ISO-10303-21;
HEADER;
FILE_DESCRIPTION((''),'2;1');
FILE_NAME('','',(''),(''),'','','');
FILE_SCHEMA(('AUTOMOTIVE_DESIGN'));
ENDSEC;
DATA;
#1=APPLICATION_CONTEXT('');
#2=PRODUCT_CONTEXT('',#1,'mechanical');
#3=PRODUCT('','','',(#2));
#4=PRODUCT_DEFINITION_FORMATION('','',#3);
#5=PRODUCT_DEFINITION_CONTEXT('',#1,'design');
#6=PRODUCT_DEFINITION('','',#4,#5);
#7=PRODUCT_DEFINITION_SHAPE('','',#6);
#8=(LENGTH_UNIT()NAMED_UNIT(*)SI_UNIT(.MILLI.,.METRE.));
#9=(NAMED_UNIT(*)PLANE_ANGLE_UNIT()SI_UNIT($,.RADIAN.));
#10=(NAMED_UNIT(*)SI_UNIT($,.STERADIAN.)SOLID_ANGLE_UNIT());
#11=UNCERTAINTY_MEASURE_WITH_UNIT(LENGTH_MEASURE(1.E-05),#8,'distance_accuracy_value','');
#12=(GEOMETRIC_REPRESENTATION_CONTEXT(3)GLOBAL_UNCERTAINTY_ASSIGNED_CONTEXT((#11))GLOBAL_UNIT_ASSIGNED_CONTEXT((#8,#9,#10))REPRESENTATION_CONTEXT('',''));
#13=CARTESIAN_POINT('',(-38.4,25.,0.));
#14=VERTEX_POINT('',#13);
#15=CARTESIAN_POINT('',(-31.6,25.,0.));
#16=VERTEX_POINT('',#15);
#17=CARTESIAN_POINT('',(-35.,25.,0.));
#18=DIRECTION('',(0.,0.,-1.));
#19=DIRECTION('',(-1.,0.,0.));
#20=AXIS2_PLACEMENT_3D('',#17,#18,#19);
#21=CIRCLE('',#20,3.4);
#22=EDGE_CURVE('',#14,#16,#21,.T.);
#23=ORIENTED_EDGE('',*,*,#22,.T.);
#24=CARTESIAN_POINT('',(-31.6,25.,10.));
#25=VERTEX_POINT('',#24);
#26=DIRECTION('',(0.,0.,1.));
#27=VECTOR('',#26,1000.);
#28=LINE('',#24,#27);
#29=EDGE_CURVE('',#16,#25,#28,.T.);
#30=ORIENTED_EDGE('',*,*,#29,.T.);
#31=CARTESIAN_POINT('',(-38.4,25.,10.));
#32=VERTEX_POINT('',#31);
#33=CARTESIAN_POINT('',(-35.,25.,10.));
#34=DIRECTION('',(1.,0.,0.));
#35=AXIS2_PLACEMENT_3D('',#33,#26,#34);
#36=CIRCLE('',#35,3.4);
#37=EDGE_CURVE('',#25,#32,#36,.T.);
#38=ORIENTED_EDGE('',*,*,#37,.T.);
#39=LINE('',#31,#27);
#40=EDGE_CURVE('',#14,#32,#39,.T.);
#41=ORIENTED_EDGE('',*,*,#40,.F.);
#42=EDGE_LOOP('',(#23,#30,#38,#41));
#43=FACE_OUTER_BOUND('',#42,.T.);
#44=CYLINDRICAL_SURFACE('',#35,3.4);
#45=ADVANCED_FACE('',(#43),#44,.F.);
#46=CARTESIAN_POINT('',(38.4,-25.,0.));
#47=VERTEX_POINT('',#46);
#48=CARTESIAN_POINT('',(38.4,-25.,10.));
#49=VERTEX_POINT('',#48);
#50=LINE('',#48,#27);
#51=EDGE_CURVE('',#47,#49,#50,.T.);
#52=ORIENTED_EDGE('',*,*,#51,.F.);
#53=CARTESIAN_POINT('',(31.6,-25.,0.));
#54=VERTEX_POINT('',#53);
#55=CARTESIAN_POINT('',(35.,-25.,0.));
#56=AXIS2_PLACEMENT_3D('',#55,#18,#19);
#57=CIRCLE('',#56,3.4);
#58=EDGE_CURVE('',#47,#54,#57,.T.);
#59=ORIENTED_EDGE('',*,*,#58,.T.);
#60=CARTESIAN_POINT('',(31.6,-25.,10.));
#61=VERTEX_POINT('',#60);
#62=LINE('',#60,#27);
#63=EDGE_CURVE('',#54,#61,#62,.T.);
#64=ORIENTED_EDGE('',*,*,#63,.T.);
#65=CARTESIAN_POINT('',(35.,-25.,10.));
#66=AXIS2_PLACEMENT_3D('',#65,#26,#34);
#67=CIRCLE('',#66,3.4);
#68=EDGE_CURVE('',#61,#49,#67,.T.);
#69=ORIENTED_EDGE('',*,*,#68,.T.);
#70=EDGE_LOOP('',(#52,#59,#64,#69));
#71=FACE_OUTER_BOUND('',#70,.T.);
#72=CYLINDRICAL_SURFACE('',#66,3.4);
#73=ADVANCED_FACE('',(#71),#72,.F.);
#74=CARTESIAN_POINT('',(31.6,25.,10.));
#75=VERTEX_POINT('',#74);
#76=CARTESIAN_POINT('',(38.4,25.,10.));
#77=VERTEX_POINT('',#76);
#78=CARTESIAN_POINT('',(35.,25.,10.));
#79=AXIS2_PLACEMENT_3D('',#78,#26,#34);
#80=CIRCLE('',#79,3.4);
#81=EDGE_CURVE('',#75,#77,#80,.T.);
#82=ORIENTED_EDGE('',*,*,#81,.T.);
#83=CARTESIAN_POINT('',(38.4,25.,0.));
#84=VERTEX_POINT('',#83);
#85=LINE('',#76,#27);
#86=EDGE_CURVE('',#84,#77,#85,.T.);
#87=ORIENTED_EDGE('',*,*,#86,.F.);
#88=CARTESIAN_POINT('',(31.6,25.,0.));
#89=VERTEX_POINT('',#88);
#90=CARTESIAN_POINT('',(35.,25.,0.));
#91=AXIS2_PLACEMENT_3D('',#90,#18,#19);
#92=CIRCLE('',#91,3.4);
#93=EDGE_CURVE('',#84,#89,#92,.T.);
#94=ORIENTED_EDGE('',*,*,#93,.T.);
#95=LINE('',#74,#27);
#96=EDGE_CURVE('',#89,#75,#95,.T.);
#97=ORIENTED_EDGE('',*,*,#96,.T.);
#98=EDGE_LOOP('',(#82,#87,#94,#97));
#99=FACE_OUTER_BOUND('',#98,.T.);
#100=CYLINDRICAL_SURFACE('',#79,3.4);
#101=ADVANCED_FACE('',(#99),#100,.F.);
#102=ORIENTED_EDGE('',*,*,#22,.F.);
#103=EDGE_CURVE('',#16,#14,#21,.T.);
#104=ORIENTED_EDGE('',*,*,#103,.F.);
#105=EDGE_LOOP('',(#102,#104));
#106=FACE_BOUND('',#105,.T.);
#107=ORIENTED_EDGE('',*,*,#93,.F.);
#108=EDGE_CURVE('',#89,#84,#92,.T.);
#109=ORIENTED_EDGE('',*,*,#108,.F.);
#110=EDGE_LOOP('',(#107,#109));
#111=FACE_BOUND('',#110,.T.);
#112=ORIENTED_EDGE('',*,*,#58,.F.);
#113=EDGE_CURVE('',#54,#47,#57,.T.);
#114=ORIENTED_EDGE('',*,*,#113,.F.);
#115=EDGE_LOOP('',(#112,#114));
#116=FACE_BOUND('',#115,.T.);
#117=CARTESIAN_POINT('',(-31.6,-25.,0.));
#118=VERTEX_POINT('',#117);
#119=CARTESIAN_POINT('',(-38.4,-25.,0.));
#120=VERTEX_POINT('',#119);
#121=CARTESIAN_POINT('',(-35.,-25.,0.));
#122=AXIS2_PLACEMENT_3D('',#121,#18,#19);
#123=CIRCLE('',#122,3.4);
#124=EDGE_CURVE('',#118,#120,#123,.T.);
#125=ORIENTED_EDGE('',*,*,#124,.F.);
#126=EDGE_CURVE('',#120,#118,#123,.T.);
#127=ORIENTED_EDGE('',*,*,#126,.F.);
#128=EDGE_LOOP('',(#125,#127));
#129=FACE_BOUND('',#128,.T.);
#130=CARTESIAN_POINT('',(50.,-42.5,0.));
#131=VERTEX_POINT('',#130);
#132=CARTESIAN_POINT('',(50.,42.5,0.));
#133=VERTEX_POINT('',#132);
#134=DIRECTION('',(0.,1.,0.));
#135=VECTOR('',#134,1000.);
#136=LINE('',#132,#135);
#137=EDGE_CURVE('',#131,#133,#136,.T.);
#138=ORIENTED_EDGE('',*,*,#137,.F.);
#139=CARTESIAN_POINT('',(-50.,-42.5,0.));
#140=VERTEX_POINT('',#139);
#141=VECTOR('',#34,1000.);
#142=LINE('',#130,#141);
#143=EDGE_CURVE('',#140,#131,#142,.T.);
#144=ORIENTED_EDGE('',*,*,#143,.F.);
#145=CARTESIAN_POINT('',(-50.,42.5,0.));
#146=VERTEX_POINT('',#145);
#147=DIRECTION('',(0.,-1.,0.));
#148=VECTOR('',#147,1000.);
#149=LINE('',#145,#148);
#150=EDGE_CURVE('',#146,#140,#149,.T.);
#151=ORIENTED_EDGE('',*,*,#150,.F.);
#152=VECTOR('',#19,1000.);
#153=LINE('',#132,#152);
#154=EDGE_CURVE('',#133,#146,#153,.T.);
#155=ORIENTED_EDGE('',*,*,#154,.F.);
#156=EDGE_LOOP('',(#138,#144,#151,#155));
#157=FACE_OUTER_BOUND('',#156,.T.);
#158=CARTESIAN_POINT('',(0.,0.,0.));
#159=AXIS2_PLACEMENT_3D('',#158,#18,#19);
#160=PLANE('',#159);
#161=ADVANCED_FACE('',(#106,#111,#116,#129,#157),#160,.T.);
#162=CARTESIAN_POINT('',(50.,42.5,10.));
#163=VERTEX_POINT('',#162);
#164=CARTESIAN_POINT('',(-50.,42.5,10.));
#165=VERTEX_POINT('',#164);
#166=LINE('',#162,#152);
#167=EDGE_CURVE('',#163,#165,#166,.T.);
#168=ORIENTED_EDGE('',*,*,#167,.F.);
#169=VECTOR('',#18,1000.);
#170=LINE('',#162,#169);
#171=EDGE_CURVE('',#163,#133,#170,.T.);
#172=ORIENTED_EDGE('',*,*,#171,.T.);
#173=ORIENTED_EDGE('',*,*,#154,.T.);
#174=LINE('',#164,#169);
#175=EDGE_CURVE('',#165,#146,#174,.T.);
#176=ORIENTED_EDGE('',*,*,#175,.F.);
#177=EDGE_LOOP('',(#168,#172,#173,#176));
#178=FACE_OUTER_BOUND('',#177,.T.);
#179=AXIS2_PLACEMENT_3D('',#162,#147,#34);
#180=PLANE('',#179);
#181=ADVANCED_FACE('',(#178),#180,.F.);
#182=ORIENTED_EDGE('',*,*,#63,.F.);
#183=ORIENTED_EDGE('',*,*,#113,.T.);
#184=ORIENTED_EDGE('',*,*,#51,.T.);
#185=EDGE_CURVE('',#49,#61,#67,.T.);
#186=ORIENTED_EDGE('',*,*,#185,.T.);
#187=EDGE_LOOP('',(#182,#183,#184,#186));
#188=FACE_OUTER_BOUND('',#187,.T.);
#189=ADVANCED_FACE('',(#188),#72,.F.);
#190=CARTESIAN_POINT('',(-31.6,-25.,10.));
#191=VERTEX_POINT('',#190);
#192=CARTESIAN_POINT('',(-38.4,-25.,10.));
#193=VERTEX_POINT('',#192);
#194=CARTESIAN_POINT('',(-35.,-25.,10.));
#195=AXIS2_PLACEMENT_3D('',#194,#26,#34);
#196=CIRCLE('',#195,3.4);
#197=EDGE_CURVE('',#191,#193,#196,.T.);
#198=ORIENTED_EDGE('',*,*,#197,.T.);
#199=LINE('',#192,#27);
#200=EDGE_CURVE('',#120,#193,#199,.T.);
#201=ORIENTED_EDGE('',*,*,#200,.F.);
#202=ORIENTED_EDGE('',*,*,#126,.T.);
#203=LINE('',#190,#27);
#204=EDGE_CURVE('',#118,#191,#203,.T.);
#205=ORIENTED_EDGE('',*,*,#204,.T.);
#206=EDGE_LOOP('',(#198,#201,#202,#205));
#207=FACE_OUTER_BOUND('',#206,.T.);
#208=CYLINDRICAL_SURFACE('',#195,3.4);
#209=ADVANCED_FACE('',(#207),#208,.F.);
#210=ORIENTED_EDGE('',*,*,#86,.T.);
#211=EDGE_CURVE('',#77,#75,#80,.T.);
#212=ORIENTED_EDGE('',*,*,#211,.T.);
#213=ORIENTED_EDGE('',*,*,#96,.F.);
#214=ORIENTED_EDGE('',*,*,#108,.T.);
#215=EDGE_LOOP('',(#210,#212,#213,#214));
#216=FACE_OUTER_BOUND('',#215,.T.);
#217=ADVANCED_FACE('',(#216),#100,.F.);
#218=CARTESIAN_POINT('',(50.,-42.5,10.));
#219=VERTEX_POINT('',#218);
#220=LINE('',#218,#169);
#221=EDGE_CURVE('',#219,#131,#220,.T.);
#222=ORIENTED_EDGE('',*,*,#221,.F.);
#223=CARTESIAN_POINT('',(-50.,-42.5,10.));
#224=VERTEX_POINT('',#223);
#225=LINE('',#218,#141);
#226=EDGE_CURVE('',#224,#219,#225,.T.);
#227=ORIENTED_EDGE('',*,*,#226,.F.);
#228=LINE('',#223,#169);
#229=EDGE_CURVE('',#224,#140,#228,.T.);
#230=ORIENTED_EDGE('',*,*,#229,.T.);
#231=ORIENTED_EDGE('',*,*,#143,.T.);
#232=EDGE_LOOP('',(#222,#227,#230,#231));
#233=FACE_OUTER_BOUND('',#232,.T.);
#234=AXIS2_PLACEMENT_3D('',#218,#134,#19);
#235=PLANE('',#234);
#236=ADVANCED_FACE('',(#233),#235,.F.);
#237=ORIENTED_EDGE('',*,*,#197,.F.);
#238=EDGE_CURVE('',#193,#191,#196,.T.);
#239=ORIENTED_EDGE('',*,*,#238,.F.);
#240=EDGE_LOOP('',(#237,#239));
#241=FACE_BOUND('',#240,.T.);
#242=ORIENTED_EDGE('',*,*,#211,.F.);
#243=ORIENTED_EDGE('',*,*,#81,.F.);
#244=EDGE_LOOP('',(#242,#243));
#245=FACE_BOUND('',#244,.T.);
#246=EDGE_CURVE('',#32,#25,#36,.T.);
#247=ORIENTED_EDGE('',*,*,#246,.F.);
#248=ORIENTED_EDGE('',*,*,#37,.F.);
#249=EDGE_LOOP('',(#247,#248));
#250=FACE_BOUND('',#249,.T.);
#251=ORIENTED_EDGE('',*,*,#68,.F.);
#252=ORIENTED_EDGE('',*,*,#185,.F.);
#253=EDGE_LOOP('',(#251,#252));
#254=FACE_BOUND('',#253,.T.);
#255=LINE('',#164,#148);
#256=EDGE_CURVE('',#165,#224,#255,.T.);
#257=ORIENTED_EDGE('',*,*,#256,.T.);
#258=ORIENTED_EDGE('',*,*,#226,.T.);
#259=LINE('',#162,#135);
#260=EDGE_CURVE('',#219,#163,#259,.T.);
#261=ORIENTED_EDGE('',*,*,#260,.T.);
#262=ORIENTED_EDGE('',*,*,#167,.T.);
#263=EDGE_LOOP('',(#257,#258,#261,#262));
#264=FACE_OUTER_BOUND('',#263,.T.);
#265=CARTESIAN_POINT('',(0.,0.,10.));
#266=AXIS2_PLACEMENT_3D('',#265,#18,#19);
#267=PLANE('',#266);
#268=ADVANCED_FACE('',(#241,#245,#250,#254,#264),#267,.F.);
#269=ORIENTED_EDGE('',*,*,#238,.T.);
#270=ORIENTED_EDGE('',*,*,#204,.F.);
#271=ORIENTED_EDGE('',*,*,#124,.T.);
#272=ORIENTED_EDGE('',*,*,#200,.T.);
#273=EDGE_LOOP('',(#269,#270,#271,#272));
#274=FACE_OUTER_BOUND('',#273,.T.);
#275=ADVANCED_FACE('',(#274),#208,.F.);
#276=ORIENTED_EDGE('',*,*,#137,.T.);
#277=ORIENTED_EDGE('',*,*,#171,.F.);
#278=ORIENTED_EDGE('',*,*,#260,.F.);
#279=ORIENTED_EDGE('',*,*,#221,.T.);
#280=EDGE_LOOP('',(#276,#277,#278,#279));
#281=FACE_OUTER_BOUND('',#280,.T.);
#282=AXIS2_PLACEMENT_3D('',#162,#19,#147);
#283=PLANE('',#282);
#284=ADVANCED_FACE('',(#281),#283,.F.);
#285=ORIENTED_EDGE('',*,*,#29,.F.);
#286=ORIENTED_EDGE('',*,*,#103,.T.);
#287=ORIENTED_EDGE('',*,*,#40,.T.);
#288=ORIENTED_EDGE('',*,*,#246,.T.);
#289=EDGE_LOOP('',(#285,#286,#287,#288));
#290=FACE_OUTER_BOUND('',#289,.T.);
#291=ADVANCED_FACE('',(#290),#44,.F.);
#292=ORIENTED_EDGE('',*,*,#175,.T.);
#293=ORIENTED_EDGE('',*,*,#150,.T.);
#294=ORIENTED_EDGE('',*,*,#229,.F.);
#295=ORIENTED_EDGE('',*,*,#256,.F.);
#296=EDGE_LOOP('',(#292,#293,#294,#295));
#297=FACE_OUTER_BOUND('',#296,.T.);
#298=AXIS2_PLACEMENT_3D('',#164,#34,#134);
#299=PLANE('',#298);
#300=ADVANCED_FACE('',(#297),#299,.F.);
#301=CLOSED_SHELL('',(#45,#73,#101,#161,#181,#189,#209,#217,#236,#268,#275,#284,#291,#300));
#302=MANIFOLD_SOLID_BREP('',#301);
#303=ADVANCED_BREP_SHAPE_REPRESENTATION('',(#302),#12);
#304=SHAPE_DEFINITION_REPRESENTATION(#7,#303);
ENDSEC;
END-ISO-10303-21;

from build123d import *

# Parameters (mm, degrees)
SKETCH1_W             = 100
SKETCH1_H             = 85
BOSS_EXTRUDE1_DEPTH   = 10
M8_TAPPED_HOLE1_D     = 6.8
M8_TAPPED_HOLE1_DEPTH = 19.75
M8_TAPPED_HOLE1_TIP   = 2.042926105


with BuildPart() as part:
    # Sketch1 → Boss-Extrude1 (new body)
    with BuildSketch(Plane.XY):
        Rectangle(SKETCH1_W, SKETCH1_H)
    extrude(amount=BOSS_EXTRUDE1_DEPTH)

    # M8 Tapped Hole1
    with Locations(Plane.XY.offset(10)):
        with Locations((-35, 25), (35, 25), (35, -25), (-35, -25)):
            Hole(M8_TAPPED_HOLE1_D / 2, depth=M8_TAPPED_HOLE1_DEPTH)
            with Locations((0, 0, -(M8_TAPPED_HOLE1_DEPTH + M8_TAPPED_HOLE1_TIP / 2))):  # 118° drill point
                Cone(0, M8_TAPPED_HOLE1_D / 2, M8_TAPPED_HOLE1_TIP, mode=Mode.SUBTRACT)


solid = part.part
